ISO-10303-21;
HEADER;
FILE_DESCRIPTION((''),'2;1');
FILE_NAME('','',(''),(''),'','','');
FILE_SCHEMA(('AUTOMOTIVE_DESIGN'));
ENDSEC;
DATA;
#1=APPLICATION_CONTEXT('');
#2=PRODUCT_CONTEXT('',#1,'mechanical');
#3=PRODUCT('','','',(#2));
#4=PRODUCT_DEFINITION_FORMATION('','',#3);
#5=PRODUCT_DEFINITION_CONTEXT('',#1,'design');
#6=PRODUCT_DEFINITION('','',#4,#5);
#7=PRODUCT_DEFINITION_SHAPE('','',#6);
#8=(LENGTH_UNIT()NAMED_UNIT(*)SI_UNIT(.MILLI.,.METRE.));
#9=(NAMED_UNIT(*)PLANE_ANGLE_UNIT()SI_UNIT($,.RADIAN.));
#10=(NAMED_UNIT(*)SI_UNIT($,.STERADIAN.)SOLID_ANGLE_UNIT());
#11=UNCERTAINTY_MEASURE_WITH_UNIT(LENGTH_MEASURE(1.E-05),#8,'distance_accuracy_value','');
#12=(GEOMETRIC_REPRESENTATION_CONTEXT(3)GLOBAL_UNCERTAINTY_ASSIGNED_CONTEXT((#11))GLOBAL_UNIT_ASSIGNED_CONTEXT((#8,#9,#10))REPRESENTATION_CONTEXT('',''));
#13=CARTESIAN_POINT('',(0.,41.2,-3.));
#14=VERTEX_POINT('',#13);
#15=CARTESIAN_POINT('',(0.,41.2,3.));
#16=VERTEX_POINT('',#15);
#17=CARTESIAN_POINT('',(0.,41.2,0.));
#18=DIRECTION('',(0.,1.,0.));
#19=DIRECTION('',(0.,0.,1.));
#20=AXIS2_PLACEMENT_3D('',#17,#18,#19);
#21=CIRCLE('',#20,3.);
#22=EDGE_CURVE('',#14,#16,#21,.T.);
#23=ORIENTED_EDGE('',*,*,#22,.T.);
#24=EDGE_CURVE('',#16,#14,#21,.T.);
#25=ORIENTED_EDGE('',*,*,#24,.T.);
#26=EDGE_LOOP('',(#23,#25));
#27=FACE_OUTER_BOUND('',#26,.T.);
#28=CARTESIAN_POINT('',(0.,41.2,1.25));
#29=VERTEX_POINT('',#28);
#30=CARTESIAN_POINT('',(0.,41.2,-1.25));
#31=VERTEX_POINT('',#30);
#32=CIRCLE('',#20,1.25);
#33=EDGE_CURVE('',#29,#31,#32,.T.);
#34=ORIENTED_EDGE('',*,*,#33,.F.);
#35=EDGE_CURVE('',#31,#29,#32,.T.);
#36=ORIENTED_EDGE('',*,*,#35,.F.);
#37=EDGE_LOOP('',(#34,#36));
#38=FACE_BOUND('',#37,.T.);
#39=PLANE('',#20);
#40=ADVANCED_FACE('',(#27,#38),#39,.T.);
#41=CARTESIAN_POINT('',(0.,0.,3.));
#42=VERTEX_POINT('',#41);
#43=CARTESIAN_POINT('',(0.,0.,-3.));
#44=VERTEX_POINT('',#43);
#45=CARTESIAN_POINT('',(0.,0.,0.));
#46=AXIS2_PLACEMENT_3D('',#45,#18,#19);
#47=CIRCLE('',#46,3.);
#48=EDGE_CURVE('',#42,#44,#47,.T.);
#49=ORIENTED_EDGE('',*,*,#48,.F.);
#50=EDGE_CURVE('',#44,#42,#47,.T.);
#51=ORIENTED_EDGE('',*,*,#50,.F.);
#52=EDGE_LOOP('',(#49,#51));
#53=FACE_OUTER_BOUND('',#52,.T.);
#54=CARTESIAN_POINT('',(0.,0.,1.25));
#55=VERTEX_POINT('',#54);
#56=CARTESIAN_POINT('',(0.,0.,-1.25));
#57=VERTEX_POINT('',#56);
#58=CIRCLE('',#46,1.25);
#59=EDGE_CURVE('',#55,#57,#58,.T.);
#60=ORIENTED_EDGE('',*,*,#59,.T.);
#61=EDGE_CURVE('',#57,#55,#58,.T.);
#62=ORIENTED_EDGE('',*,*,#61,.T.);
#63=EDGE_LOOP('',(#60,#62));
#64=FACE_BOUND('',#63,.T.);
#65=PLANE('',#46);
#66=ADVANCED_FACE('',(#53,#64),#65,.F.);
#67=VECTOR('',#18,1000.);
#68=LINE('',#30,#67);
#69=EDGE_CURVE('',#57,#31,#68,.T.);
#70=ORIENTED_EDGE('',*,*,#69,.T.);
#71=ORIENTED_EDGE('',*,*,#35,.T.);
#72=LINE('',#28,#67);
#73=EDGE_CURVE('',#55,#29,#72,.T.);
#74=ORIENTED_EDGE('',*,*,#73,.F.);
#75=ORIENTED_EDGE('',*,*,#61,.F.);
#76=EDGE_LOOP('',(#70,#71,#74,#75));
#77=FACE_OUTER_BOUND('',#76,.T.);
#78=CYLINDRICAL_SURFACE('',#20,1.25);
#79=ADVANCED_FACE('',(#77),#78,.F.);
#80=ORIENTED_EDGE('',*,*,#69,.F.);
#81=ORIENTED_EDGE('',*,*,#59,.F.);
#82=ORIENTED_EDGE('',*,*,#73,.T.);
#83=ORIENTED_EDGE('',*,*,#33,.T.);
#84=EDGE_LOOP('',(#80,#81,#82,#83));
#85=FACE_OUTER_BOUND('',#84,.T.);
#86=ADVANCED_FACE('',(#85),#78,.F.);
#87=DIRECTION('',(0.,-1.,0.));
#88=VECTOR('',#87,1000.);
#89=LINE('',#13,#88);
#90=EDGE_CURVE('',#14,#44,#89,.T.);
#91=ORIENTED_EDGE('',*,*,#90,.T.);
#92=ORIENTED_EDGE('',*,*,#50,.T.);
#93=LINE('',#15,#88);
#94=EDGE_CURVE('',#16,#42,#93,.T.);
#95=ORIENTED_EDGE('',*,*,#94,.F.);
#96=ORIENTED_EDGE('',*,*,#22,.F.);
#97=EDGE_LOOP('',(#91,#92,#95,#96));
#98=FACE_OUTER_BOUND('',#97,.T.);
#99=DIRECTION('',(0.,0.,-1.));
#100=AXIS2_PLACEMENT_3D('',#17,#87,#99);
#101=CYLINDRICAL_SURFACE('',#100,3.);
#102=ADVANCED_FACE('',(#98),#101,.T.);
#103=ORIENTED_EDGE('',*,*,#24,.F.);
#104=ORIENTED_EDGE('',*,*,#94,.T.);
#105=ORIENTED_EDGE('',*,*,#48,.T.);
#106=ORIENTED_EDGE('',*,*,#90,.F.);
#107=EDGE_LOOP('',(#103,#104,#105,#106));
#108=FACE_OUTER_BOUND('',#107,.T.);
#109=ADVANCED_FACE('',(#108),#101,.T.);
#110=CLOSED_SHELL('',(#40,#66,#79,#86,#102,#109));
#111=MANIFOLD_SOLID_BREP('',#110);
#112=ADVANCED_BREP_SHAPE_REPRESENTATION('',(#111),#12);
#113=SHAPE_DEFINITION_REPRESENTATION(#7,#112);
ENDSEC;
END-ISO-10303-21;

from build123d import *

# Parameters (mm, degrees)
SKETCH_1_R         = 3
EXTRUDE_1_DEPTH    = 41.2
HOLE_WIZARD_M3_1_D = 2.5


with BuildPart() as part:
    # 草图1 → 凸台-拉伸1 (new body)
    with BuildSketch(Plane(origin=(0, 0, 0), x_dir=(1, 0, 0), z_dir=(0, 1, 0))):
        with Locations(Location((0, 0, 0), (0, 0, 90))):
            Circle(SKETCH_1_R)
    extrude(amount=EXTRUDE_1_DEPTH)

    # M3 螺纹孔1 (through all)
    with Locations(Plane(origin=(0, 41.2, 0), x_dir=(1, 0, 0), z_dir=(0, 1, 0))):
        with Locations((0, 0)):
            Hole(HOLE_WIZARD_M3_1_D / 2)


solid = part.part
